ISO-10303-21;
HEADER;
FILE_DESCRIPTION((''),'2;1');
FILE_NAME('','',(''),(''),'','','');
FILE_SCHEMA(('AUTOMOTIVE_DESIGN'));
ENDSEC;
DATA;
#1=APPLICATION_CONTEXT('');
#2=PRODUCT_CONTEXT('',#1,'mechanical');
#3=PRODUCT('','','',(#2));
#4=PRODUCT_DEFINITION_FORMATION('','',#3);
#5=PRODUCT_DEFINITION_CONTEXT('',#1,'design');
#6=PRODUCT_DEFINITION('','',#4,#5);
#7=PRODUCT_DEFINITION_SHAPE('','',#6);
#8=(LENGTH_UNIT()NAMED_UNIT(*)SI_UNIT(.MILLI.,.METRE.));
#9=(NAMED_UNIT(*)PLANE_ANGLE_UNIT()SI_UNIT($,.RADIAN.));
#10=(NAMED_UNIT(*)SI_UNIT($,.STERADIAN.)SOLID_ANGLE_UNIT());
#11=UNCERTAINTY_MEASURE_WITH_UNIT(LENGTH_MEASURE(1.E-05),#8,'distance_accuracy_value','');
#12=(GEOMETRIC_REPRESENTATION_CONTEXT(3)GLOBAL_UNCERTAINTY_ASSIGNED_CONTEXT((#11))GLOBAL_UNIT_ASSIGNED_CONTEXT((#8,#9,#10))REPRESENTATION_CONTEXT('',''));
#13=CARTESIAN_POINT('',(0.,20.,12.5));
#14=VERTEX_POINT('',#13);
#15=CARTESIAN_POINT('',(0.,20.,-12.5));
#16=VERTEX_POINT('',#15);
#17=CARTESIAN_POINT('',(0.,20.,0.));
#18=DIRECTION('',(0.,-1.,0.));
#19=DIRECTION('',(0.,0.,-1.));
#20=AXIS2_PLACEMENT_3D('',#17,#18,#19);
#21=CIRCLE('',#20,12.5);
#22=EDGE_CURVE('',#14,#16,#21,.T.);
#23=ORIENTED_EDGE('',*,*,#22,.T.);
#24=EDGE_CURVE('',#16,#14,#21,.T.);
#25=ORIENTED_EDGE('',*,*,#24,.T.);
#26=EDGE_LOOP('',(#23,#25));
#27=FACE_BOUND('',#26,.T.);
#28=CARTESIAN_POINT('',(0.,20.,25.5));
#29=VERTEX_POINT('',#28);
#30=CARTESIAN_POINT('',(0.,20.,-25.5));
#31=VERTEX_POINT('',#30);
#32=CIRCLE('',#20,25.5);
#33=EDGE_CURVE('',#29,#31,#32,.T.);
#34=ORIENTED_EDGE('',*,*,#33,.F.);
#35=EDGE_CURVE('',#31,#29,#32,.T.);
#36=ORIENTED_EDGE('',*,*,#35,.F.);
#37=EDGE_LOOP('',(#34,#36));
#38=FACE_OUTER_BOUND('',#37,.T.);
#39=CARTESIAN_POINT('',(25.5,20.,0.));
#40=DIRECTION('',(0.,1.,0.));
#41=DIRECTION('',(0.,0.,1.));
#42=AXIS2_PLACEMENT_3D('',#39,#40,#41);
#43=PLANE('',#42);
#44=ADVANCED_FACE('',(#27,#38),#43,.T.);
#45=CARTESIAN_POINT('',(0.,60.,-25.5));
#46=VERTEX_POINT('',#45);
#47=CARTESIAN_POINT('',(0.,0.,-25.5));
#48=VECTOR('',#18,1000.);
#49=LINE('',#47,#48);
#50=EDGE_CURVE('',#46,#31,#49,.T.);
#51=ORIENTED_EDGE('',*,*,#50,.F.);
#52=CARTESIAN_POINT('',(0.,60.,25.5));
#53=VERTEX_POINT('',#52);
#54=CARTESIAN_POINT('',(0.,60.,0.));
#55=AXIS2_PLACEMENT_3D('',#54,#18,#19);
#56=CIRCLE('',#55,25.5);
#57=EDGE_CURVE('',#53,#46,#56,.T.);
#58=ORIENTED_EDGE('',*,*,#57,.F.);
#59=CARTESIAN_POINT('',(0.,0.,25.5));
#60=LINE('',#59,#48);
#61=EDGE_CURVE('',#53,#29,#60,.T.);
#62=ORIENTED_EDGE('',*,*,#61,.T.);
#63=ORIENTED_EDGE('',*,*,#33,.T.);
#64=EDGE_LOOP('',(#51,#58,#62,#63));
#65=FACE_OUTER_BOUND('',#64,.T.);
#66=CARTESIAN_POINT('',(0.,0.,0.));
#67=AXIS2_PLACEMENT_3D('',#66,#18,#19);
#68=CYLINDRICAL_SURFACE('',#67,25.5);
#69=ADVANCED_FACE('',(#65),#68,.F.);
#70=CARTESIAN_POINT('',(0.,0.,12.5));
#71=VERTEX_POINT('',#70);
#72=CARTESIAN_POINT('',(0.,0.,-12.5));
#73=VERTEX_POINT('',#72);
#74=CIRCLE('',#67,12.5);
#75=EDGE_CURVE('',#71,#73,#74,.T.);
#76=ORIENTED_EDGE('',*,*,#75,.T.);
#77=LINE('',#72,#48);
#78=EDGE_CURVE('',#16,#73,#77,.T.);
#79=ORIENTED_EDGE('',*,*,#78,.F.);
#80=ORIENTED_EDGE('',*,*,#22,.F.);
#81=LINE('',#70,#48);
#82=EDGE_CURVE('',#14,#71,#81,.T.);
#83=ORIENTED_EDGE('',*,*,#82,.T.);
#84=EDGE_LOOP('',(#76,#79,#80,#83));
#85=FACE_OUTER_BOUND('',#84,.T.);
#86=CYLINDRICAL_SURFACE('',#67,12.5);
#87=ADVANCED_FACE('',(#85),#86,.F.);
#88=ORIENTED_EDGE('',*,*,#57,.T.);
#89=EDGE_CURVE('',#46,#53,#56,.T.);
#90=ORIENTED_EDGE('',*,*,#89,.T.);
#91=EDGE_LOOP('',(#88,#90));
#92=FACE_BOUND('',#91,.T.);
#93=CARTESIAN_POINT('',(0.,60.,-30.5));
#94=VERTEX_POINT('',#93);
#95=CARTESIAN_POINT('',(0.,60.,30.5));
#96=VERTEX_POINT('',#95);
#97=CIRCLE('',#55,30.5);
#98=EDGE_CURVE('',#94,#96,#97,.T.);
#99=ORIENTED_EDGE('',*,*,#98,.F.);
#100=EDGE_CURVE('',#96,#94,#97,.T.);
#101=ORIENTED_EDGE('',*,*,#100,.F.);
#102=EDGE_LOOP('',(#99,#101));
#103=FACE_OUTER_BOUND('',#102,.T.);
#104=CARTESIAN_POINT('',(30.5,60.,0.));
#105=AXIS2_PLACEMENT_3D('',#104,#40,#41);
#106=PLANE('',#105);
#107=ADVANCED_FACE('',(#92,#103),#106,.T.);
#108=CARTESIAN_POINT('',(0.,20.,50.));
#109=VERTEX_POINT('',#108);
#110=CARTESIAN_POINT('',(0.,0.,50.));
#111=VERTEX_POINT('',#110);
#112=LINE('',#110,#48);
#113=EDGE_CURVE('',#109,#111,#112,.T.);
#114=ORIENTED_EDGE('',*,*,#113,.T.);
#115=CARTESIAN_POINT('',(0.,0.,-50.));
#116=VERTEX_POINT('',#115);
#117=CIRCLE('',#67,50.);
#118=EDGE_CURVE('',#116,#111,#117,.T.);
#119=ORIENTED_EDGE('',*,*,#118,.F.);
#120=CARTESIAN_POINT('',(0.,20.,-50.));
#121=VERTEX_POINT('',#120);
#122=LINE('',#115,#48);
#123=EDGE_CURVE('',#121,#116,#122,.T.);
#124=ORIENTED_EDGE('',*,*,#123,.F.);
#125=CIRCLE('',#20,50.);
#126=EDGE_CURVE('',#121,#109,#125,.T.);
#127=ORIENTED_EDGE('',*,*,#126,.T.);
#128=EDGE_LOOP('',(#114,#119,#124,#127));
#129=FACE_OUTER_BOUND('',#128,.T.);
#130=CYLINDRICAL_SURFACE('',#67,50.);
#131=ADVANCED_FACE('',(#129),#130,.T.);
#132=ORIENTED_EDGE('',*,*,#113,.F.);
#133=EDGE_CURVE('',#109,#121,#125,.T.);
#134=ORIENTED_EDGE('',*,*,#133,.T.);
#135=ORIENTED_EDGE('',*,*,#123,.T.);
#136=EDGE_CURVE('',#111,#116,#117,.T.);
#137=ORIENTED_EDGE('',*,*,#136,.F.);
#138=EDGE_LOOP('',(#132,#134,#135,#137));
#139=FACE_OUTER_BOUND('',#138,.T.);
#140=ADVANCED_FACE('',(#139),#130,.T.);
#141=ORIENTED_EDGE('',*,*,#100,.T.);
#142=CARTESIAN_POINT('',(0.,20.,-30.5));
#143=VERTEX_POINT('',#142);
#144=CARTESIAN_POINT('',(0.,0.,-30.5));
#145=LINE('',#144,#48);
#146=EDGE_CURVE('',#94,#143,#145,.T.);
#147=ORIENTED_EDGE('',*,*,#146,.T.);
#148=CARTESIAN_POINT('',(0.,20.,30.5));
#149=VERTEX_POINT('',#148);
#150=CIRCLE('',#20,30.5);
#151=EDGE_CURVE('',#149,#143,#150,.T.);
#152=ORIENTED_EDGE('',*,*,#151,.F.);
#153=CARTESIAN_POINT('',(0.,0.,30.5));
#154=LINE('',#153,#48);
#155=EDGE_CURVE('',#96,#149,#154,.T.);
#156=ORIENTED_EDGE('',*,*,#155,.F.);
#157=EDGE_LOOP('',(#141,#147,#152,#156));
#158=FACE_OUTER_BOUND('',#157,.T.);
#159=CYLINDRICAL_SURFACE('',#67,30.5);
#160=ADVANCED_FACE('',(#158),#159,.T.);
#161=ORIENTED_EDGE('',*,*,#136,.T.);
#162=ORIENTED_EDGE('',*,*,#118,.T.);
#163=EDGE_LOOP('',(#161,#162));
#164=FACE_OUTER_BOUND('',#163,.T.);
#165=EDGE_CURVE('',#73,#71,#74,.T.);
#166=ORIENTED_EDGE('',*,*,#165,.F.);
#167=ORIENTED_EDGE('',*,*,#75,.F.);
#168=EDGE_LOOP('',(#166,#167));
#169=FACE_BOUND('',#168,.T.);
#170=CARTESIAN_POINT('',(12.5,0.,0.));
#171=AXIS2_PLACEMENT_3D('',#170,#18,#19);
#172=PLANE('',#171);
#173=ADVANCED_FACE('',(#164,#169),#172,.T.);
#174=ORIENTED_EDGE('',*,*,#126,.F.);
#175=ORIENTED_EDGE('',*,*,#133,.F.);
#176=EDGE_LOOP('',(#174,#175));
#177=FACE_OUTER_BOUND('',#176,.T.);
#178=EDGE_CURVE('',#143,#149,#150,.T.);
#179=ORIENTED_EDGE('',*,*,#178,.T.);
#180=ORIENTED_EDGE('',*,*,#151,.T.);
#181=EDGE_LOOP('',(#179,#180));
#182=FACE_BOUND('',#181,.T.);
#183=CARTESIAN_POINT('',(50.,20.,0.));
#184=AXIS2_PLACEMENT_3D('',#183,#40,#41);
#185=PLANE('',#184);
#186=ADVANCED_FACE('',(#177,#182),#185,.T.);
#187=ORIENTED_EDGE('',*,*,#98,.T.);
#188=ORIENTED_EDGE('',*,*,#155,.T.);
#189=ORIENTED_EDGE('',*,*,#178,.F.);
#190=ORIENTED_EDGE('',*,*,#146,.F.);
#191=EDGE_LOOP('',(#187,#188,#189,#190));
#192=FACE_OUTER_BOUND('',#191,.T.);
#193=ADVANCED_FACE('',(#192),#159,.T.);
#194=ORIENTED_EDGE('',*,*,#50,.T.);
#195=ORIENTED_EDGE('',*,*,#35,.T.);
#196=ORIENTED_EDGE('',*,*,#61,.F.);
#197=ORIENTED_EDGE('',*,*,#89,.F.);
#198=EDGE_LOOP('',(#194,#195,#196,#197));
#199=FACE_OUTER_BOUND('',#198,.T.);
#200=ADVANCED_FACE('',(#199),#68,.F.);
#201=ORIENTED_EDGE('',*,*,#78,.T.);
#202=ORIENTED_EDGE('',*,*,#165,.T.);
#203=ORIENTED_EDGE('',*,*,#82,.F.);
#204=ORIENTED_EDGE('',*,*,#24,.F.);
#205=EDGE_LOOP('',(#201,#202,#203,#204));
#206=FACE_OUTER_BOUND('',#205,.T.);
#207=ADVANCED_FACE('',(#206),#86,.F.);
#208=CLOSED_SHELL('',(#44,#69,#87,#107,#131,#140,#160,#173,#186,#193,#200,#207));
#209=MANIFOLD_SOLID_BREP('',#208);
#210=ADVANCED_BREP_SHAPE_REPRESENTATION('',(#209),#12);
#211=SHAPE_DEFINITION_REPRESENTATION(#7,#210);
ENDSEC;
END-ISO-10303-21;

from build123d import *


with BuildPart() as part:
    # Sketch1 → Revolve1 (revolve)
    with BuildSketch(Plane.XY, mode=Mode.PRIVATE) as revolve1_sk:
        Polygon((25.5, 60), (25.5, 20), (12.5, 20), (12.5, 0), (50, 0), (50, 20), (30.5, 20), (30.5, 60), align=None)
    revolve(revolve1_sk.sketch.rotate(Axis((0, 0, 0), (0, 1, 0)), 90), axis=Axis((0, 0, 0), (0, 1, 0)))


solid = part.part
